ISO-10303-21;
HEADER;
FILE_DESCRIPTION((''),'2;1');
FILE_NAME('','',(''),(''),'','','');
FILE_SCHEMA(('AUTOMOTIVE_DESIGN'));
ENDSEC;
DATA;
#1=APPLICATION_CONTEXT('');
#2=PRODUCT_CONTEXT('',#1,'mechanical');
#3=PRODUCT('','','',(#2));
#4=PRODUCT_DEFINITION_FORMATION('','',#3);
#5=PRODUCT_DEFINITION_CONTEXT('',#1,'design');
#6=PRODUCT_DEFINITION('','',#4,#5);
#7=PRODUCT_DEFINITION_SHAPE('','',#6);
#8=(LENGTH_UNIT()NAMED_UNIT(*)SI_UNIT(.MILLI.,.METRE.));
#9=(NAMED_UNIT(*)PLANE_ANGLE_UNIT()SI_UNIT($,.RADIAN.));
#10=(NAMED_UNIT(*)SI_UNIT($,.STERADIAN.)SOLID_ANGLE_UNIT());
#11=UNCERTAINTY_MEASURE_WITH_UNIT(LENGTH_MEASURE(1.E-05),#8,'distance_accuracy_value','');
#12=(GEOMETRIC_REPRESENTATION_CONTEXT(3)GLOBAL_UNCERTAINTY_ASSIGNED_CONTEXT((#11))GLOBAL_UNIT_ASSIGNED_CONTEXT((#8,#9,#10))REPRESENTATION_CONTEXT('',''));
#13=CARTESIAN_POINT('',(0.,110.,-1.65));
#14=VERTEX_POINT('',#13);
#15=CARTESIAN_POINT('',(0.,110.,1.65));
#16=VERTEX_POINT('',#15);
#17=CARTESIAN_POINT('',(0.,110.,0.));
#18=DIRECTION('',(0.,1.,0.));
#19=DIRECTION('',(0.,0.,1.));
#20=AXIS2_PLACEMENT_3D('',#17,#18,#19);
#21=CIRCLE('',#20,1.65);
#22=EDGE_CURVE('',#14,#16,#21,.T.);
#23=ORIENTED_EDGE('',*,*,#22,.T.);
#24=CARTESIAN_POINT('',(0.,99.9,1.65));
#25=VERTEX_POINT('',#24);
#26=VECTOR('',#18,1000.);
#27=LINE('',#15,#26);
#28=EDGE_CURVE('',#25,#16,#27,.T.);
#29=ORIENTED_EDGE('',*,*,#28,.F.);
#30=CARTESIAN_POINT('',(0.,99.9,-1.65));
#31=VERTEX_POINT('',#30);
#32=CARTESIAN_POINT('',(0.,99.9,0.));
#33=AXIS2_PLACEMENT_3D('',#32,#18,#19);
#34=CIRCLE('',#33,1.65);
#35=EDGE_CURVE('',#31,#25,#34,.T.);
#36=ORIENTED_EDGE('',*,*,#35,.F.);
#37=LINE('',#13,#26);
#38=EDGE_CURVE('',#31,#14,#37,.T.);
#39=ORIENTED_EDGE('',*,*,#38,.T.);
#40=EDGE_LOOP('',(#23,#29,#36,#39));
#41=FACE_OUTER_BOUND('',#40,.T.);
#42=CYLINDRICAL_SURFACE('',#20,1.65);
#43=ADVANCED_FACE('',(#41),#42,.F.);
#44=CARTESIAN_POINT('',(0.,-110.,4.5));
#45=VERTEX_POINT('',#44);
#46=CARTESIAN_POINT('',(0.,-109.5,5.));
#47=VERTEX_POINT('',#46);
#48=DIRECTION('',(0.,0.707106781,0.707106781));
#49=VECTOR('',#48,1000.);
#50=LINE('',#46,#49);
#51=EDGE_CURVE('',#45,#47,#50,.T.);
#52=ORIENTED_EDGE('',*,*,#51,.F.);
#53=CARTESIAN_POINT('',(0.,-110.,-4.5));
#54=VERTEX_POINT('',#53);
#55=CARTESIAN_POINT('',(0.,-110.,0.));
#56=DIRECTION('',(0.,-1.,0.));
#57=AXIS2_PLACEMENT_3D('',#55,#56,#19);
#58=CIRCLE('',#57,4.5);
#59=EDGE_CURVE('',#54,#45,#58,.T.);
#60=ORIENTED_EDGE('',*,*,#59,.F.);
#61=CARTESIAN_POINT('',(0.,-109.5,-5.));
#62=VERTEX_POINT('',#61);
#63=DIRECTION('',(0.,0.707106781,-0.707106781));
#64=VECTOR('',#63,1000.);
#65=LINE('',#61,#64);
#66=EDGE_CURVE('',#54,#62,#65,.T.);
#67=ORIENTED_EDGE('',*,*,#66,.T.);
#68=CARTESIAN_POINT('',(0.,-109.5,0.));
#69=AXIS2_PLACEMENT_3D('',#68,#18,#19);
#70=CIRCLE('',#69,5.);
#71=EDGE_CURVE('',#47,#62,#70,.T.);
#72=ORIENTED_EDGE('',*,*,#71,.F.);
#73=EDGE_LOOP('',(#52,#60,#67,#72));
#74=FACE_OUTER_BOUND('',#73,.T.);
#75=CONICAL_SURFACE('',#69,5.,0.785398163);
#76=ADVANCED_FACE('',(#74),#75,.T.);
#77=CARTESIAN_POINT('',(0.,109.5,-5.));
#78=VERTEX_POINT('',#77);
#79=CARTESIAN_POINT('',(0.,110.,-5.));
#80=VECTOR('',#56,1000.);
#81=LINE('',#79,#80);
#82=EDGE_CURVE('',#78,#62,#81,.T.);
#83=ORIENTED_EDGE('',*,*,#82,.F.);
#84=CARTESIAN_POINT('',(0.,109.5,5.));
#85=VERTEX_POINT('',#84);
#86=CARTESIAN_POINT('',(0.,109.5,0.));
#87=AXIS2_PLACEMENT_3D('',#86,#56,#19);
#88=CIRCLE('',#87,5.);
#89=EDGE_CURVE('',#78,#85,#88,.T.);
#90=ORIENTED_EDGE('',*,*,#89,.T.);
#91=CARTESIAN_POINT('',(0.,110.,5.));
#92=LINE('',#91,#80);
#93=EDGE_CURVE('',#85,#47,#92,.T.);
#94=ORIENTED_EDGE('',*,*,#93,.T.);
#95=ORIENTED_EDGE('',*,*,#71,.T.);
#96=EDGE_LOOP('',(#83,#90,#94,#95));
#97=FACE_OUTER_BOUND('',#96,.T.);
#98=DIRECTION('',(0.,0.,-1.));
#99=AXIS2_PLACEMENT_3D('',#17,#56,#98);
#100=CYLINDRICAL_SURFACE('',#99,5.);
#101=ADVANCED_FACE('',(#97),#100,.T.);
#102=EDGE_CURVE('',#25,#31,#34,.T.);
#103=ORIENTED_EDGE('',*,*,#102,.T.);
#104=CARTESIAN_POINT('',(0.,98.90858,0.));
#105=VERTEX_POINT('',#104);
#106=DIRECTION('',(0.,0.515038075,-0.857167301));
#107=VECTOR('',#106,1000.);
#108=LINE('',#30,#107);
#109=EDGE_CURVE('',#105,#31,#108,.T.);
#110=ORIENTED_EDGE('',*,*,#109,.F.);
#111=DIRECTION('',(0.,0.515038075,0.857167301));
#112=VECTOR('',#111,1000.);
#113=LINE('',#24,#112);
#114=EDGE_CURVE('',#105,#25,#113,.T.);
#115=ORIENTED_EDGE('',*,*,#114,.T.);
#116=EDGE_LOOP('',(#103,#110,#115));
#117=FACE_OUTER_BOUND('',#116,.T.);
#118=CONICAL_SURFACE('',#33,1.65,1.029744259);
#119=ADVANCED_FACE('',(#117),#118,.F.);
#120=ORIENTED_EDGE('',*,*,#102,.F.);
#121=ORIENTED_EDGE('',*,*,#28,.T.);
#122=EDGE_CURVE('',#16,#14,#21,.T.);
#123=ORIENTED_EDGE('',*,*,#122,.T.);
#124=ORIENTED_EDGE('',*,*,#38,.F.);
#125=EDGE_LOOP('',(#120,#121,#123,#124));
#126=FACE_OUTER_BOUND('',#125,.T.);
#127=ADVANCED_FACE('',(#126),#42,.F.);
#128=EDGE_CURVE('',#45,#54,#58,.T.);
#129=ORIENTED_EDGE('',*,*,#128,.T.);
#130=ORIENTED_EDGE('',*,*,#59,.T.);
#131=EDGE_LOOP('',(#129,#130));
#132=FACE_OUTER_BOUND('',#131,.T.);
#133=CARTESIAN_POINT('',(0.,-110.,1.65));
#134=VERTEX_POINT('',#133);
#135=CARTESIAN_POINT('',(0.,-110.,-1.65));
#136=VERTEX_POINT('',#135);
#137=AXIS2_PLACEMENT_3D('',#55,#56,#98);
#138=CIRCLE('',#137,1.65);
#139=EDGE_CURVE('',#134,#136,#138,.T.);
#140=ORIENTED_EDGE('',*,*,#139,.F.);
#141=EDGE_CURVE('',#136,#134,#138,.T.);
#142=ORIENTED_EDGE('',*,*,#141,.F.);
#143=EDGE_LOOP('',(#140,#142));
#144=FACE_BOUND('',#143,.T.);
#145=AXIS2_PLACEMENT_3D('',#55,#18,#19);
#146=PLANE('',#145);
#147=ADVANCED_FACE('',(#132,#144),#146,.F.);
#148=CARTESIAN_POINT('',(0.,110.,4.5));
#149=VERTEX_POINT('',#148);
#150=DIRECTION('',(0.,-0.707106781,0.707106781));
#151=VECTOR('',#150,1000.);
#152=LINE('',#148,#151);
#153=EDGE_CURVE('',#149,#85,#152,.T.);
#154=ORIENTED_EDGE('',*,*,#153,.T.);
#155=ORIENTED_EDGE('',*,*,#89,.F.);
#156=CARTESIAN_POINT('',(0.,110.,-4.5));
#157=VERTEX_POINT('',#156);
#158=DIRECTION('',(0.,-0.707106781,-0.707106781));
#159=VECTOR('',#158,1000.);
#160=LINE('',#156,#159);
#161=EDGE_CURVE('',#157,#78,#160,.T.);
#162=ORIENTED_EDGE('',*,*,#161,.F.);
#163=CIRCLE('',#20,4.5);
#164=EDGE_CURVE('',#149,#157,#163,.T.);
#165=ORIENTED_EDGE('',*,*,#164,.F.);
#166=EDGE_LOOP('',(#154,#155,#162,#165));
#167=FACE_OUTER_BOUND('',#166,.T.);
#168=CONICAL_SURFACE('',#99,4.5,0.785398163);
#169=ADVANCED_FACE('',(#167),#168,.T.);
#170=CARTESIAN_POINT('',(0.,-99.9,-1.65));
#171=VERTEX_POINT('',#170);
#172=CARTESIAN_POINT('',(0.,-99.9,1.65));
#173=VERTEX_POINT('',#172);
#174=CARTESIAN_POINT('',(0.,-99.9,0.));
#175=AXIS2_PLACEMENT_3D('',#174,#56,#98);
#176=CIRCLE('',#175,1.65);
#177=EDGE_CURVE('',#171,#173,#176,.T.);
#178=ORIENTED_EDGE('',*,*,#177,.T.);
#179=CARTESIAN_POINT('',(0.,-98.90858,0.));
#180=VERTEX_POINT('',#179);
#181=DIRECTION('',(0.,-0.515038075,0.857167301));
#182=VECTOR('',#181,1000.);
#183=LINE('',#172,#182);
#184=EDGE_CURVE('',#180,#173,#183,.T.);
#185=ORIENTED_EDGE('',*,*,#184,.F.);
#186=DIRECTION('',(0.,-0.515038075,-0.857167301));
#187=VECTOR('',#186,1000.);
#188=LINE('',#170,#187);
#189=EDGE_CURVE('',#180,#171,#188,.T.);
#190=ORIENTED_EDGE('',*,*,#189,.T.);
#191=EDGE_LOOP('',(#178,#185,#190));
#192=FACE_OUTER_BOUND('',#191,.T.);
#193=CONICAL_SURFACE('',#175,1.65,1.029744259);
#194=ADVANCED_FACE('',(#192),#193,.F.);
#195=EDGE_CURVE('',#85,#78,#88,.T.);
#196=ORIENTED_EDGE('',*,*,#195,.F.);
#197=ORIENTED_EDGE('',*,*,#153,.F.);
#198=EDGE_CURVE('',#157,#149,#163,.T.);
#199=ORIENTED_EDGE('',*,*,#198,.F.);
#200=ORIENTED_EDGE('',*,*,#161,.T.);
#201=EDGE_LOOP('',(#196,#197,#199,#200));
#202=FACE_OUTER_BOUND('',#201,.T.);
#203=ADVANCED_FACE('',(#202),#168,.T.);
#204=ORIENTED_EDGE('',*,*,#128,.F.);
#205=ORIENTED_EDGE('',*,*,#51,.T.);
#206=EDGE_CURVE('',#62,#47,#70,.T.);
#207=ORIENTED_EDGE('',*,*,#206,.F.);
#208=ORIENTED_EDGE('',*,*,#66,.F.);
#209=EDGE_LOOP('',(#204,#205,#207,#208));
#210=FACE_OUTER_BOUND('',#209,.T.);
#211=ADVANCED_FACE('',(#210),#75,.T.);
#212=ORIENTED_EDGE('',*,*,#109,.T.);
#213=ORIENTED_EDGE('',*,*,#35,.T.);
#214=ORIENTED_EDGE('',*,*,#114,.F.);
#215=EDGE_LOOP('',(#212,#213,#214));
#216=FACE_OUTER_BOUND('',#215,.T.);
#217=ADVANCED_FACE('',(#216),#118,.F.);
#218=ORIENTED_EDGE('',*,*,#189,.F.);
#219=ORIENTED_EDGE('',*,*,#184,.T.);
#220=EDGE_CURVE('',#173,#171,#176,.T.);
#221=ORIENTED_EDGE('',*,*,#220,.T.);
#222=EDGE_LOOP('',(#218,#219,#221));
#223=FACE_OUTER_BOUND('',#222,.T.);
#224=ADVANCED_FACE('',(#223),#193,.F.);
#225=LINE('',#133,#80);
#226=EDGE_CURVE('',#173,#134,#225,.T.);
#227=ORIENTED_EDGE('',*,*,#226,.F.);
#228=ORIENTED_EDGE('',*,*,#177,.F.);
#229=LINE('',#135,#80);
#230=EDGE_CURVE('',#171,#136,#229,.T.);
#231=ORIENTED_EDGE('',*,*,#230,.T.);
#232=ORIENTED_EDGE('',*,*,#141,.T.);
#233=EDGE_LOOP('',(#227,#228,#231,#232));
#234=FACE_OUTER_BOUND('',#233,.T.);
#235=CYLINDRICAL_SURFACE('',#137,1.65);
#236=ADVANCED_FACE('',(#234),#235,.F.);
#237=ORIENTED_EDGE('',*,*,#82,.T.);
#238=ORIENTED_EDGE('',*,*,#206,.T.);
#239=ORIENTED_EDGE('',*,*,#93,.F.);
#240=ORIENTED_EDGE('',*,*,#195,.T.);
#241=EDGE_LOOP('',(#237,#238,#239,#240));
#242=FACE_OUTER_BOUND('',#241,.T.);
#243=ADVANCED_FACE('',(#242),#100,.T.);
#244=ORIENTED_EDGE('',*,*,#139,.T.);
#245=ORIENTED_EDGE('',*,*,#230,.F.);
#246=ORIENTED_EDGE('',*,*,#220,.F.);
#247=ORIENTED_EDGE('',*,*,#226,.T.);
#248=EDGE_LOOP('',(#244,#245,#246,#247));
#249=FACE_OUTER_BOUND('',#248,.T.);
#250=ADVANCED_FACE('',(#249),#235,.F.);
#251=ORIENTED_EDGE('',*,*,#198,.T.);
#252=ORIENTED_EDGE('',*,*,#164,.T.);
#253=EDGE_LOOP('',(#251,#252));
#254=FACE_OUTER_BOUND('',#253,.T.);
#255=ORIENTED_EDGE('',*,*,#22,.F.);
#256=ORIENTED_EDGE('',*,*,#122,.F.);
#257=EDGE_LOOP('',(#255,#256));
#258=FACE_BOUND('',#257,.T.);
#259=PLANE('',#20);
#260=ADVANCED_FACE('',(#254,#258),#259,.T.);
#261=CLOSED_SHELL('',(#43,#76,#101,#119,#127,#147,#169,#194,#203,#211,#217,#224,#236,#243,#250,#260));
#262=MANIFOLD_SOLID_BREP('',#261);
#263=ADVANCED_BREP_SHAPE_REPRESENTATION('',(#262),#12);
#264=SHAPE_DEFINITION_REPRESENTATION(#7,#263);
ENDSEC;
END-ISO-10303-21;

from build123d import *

# Parameters (mm, degrees)
SKETCH1_R             = 5
BOSS_EXTRUDE1_DEPTH   = 110
CHAMFER1_SIZE         = 0.5
M4_TAPPED_HOLE1_D     = 3.3
M4_TAPPED_HOLE1_DEPTH = 10.1
M4_TAPPED_HOLE1_TIP   = 0.991420021
M4_TAPPED_HOLE2_D     = 3.3
M4_TAPPED_HOLE2_DEPTH = 10.1
M4_TAPPED_HOLE2_TIP   = 0.991420021


with BuildPart() as part:
    # Sketch1 → Boss-Extrude1 (new, symmetric)
    with BuildSketch(Plane(origin=(0, 0, 0), x_dir=(1, 0, 0), z_dir=(0, 1, 0))):
        with Locations(Location((0, 0, 0), (0, 0, 270))):
            Circle(SKETCH1_R)
    extrude(amount=BOSS_EXTRUDE1_DEPTH, both=True)

    # Chamfer1
    chamfer1_edges = [part.edges().sort_by_distance(p)[0] for p in [
        (0, -110, -5),
        (0, 110, -5),
    ]]
    chamfer(chamfer1_edges, length=CHAMFER1_SIZE)

    # M4 Tapped Hole1
    with Locations(Plane(origin=(0, 110, 0), x_dir=(1, 0, 0), z_dir=(0, 1, 0))):
        with Locations((0, 0)):
            Hole(M4_TAPPED_HOLE1_D / 2, depth=M4_TAPPED_HOLE1_DEPTH)
            with Locations((0, 0, -(M4_TAPPED_HOLE1_DEPTH + M4_TAPPED_HOLE1_TIP / 2))):  # 118° drill point
                Cone(0, M4_TAPPED_HOLE1_D / 2, M4_TAPPED_HOLE1_TIP, mode=Mode.SUBTRACT)

    # M4 Tapped Hole2
    with Locations(Plane(origin=(0, -110, 0), x_dir=(-1, 0, 0), z_dir=(0, -1, 0))):
        with Locations((0, 0)):
            Hole(M4_TAPPED_HOLE2_D / 2, depth=M4_TAPPED_HOLE2_DEPTH)
            with Locations((0, 0, -(M4_TAPPED_HOLE2_DEPTH + M4_TAPPED_HOLE2_TIP / 2))):  # 118° drill point
                Cone(0, M4_TAPPED_HOLE2_D / 2, M4_TAPPED_HOLE2_TIP, mode=Mode.SUBTRACT)


solid = part.part
